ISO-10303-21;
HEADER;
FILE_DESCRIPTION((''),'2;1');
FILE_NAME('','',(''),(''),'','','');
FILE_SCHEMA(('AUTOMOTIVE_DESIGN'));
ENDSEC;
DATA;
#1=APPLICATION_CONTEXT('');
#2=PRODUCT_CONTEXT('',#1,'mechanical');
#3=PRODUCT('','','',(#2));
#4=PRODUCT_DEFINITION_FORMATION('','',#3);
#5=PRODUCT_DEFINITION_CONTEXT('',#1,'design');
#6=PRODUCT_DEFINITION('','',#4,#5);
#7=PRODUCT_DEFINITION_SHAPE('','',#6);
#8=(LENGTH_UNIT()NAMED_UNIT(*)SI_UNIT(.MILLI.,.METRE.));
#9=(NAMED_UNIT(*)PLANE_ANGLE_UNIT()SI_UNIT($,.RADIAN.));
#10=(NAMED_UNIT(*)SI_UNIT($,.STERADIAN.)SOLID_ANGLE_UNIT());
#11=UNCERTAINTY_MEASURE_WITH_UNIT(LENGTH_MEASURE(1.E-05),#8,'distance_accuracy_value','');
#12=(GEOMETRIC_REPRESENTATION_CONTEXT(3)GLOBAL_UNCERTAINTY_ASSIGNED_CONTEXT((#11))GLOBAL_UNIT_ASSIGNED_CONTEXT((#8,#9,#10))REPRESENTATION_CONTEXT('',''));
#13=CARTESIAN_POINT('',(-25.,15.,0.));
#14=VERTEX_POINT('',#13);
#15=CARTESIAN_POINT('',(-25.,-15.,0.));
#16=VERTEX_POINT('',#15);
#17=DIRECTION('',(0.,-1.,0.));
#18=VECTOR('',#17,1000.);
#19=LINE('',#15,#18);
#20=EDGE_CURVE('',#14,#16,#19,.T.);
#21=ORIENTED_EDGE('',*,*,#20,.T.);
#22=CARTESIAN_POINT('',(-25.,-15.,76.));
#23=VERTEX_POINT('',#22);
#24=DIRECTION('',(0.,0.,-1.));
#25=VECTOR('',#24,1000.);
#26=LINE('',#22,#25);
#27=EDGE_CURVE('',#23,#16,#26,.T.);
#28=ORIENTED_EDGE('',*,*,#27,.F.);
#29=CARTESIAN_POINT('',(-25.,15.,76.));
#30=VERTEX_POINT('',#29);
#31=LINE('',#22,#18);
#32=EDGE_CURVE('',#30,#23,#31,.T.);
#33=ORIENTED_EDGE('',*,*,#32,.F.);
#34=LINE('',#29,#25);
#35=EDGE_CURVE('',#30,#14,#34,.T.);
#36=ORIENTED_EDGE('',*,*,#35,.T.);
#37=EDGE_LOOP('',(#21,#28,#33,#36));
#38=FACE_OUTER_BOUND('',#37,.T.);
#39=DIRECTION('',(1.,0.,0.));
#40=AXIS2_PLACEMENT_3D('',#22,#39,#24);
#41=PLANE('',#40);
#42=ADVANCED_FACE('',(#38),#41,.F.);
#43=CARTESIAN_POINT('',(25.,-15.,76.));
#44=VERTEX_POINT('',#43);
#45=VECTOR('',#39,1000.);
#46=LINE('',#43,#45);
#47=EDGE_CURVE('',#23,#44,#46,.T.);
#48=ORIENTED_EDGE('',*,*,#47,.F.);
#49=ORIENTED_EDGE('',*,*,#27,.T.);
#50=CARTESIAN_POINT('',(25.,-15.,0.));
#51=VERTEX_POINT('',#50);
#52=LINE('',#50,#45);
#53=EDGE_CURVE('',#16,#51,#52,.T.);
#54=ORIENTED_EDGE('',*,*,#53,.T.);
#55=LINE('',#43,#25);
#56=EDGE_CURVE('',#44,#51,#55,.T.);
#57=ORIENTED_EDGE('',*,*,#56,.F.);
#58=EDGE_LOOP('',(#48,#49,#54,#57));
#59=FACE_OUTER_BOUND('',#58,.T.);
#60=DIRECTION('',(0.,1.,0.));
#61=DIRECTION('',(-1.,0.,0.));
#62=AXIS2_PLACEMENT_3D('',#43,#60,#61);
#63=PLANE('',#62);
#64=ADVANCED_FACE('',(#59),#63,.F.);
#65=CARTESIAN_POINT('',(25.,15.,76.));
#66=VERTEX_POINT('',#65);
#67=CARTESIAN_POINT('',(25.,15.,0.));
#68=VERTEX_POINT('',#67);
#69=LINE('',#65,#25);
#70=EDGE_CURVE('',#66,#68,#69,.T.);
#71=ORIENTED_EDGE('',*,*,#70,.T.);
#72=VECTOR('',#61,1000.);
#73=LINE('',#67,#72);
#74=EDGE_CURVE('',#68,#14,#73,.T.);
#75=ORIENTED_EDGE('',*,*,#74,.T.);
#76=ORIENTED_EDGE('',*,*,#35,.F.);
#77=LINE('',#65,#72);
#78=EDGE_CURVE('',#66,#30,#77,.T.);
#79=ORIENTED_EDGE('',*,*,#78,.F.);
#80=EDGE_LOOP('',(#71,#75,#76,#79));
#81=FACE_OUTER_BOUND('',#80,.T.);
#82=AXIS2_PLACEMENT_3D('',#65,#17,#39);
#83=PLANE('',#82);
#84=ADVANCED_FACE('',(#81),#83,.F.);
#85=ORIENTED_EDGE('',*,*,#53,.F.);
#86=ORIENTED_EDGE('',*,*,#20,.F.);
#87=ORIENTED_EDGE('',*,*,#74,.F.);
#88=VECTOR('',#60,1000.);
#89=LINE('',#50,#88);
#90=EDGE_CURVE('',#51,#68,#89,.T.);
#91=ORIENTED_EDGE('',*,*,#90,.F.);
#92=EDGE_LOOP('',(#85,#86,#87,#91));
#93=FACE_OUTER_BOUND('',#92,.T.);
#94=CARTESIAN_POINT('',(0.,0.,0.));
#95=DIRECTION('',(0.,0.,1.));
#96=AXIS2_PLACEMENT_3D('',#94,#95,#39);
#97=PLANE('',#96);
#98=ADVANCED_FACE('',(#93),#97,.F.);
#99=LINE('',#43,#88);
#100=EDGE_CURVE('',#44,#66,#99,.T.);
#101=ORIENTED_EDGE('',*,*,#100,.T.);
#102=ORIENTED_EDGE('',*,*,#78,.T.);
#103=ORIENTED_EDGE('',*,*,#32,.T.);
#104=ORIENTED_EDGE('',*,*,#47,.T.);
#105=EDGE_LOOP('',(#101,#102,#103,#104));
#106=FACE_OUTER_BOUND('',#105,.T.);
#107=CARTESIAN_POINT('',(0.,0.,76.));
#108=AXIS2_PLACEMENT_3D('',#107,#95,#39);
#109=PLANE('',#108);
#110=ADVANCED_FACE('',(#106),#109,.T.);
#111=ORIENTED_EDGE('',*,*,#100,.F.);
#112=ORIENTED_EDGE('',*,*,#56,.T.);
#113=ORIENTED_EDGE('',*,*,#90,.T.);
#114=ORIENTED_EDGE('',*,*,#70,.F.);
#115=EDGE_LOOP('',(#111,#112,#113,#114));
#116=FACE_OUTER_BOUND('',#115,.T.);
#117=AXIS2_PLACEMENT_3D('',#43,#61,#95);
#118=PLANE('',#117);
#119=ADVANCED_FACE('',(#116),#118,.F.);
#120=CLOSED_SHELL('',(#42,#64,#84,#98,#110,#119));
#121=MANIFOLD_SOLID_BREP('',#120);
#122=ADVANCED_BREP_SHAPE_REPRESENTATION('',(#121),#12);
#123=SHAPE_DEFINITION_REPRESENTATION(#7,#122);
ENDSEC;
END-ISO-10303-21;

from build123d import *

# Parameters (mm, degrees)
SKETCH1_W           = 50
SKETCH1_H           = 30
BOSS_EXTRUDE1_DEPTH = 76


with BuildPart() as part:
    # Sketch1 → Boss-Extrude1 (new body)
    with BuildSketch(Plane.XY):
        Rectangle(SKETCH1_W, SKETCH1_H)
    extrude(amount=BOSS_EXTRUDE1_DEPTH)


solid = part.part
